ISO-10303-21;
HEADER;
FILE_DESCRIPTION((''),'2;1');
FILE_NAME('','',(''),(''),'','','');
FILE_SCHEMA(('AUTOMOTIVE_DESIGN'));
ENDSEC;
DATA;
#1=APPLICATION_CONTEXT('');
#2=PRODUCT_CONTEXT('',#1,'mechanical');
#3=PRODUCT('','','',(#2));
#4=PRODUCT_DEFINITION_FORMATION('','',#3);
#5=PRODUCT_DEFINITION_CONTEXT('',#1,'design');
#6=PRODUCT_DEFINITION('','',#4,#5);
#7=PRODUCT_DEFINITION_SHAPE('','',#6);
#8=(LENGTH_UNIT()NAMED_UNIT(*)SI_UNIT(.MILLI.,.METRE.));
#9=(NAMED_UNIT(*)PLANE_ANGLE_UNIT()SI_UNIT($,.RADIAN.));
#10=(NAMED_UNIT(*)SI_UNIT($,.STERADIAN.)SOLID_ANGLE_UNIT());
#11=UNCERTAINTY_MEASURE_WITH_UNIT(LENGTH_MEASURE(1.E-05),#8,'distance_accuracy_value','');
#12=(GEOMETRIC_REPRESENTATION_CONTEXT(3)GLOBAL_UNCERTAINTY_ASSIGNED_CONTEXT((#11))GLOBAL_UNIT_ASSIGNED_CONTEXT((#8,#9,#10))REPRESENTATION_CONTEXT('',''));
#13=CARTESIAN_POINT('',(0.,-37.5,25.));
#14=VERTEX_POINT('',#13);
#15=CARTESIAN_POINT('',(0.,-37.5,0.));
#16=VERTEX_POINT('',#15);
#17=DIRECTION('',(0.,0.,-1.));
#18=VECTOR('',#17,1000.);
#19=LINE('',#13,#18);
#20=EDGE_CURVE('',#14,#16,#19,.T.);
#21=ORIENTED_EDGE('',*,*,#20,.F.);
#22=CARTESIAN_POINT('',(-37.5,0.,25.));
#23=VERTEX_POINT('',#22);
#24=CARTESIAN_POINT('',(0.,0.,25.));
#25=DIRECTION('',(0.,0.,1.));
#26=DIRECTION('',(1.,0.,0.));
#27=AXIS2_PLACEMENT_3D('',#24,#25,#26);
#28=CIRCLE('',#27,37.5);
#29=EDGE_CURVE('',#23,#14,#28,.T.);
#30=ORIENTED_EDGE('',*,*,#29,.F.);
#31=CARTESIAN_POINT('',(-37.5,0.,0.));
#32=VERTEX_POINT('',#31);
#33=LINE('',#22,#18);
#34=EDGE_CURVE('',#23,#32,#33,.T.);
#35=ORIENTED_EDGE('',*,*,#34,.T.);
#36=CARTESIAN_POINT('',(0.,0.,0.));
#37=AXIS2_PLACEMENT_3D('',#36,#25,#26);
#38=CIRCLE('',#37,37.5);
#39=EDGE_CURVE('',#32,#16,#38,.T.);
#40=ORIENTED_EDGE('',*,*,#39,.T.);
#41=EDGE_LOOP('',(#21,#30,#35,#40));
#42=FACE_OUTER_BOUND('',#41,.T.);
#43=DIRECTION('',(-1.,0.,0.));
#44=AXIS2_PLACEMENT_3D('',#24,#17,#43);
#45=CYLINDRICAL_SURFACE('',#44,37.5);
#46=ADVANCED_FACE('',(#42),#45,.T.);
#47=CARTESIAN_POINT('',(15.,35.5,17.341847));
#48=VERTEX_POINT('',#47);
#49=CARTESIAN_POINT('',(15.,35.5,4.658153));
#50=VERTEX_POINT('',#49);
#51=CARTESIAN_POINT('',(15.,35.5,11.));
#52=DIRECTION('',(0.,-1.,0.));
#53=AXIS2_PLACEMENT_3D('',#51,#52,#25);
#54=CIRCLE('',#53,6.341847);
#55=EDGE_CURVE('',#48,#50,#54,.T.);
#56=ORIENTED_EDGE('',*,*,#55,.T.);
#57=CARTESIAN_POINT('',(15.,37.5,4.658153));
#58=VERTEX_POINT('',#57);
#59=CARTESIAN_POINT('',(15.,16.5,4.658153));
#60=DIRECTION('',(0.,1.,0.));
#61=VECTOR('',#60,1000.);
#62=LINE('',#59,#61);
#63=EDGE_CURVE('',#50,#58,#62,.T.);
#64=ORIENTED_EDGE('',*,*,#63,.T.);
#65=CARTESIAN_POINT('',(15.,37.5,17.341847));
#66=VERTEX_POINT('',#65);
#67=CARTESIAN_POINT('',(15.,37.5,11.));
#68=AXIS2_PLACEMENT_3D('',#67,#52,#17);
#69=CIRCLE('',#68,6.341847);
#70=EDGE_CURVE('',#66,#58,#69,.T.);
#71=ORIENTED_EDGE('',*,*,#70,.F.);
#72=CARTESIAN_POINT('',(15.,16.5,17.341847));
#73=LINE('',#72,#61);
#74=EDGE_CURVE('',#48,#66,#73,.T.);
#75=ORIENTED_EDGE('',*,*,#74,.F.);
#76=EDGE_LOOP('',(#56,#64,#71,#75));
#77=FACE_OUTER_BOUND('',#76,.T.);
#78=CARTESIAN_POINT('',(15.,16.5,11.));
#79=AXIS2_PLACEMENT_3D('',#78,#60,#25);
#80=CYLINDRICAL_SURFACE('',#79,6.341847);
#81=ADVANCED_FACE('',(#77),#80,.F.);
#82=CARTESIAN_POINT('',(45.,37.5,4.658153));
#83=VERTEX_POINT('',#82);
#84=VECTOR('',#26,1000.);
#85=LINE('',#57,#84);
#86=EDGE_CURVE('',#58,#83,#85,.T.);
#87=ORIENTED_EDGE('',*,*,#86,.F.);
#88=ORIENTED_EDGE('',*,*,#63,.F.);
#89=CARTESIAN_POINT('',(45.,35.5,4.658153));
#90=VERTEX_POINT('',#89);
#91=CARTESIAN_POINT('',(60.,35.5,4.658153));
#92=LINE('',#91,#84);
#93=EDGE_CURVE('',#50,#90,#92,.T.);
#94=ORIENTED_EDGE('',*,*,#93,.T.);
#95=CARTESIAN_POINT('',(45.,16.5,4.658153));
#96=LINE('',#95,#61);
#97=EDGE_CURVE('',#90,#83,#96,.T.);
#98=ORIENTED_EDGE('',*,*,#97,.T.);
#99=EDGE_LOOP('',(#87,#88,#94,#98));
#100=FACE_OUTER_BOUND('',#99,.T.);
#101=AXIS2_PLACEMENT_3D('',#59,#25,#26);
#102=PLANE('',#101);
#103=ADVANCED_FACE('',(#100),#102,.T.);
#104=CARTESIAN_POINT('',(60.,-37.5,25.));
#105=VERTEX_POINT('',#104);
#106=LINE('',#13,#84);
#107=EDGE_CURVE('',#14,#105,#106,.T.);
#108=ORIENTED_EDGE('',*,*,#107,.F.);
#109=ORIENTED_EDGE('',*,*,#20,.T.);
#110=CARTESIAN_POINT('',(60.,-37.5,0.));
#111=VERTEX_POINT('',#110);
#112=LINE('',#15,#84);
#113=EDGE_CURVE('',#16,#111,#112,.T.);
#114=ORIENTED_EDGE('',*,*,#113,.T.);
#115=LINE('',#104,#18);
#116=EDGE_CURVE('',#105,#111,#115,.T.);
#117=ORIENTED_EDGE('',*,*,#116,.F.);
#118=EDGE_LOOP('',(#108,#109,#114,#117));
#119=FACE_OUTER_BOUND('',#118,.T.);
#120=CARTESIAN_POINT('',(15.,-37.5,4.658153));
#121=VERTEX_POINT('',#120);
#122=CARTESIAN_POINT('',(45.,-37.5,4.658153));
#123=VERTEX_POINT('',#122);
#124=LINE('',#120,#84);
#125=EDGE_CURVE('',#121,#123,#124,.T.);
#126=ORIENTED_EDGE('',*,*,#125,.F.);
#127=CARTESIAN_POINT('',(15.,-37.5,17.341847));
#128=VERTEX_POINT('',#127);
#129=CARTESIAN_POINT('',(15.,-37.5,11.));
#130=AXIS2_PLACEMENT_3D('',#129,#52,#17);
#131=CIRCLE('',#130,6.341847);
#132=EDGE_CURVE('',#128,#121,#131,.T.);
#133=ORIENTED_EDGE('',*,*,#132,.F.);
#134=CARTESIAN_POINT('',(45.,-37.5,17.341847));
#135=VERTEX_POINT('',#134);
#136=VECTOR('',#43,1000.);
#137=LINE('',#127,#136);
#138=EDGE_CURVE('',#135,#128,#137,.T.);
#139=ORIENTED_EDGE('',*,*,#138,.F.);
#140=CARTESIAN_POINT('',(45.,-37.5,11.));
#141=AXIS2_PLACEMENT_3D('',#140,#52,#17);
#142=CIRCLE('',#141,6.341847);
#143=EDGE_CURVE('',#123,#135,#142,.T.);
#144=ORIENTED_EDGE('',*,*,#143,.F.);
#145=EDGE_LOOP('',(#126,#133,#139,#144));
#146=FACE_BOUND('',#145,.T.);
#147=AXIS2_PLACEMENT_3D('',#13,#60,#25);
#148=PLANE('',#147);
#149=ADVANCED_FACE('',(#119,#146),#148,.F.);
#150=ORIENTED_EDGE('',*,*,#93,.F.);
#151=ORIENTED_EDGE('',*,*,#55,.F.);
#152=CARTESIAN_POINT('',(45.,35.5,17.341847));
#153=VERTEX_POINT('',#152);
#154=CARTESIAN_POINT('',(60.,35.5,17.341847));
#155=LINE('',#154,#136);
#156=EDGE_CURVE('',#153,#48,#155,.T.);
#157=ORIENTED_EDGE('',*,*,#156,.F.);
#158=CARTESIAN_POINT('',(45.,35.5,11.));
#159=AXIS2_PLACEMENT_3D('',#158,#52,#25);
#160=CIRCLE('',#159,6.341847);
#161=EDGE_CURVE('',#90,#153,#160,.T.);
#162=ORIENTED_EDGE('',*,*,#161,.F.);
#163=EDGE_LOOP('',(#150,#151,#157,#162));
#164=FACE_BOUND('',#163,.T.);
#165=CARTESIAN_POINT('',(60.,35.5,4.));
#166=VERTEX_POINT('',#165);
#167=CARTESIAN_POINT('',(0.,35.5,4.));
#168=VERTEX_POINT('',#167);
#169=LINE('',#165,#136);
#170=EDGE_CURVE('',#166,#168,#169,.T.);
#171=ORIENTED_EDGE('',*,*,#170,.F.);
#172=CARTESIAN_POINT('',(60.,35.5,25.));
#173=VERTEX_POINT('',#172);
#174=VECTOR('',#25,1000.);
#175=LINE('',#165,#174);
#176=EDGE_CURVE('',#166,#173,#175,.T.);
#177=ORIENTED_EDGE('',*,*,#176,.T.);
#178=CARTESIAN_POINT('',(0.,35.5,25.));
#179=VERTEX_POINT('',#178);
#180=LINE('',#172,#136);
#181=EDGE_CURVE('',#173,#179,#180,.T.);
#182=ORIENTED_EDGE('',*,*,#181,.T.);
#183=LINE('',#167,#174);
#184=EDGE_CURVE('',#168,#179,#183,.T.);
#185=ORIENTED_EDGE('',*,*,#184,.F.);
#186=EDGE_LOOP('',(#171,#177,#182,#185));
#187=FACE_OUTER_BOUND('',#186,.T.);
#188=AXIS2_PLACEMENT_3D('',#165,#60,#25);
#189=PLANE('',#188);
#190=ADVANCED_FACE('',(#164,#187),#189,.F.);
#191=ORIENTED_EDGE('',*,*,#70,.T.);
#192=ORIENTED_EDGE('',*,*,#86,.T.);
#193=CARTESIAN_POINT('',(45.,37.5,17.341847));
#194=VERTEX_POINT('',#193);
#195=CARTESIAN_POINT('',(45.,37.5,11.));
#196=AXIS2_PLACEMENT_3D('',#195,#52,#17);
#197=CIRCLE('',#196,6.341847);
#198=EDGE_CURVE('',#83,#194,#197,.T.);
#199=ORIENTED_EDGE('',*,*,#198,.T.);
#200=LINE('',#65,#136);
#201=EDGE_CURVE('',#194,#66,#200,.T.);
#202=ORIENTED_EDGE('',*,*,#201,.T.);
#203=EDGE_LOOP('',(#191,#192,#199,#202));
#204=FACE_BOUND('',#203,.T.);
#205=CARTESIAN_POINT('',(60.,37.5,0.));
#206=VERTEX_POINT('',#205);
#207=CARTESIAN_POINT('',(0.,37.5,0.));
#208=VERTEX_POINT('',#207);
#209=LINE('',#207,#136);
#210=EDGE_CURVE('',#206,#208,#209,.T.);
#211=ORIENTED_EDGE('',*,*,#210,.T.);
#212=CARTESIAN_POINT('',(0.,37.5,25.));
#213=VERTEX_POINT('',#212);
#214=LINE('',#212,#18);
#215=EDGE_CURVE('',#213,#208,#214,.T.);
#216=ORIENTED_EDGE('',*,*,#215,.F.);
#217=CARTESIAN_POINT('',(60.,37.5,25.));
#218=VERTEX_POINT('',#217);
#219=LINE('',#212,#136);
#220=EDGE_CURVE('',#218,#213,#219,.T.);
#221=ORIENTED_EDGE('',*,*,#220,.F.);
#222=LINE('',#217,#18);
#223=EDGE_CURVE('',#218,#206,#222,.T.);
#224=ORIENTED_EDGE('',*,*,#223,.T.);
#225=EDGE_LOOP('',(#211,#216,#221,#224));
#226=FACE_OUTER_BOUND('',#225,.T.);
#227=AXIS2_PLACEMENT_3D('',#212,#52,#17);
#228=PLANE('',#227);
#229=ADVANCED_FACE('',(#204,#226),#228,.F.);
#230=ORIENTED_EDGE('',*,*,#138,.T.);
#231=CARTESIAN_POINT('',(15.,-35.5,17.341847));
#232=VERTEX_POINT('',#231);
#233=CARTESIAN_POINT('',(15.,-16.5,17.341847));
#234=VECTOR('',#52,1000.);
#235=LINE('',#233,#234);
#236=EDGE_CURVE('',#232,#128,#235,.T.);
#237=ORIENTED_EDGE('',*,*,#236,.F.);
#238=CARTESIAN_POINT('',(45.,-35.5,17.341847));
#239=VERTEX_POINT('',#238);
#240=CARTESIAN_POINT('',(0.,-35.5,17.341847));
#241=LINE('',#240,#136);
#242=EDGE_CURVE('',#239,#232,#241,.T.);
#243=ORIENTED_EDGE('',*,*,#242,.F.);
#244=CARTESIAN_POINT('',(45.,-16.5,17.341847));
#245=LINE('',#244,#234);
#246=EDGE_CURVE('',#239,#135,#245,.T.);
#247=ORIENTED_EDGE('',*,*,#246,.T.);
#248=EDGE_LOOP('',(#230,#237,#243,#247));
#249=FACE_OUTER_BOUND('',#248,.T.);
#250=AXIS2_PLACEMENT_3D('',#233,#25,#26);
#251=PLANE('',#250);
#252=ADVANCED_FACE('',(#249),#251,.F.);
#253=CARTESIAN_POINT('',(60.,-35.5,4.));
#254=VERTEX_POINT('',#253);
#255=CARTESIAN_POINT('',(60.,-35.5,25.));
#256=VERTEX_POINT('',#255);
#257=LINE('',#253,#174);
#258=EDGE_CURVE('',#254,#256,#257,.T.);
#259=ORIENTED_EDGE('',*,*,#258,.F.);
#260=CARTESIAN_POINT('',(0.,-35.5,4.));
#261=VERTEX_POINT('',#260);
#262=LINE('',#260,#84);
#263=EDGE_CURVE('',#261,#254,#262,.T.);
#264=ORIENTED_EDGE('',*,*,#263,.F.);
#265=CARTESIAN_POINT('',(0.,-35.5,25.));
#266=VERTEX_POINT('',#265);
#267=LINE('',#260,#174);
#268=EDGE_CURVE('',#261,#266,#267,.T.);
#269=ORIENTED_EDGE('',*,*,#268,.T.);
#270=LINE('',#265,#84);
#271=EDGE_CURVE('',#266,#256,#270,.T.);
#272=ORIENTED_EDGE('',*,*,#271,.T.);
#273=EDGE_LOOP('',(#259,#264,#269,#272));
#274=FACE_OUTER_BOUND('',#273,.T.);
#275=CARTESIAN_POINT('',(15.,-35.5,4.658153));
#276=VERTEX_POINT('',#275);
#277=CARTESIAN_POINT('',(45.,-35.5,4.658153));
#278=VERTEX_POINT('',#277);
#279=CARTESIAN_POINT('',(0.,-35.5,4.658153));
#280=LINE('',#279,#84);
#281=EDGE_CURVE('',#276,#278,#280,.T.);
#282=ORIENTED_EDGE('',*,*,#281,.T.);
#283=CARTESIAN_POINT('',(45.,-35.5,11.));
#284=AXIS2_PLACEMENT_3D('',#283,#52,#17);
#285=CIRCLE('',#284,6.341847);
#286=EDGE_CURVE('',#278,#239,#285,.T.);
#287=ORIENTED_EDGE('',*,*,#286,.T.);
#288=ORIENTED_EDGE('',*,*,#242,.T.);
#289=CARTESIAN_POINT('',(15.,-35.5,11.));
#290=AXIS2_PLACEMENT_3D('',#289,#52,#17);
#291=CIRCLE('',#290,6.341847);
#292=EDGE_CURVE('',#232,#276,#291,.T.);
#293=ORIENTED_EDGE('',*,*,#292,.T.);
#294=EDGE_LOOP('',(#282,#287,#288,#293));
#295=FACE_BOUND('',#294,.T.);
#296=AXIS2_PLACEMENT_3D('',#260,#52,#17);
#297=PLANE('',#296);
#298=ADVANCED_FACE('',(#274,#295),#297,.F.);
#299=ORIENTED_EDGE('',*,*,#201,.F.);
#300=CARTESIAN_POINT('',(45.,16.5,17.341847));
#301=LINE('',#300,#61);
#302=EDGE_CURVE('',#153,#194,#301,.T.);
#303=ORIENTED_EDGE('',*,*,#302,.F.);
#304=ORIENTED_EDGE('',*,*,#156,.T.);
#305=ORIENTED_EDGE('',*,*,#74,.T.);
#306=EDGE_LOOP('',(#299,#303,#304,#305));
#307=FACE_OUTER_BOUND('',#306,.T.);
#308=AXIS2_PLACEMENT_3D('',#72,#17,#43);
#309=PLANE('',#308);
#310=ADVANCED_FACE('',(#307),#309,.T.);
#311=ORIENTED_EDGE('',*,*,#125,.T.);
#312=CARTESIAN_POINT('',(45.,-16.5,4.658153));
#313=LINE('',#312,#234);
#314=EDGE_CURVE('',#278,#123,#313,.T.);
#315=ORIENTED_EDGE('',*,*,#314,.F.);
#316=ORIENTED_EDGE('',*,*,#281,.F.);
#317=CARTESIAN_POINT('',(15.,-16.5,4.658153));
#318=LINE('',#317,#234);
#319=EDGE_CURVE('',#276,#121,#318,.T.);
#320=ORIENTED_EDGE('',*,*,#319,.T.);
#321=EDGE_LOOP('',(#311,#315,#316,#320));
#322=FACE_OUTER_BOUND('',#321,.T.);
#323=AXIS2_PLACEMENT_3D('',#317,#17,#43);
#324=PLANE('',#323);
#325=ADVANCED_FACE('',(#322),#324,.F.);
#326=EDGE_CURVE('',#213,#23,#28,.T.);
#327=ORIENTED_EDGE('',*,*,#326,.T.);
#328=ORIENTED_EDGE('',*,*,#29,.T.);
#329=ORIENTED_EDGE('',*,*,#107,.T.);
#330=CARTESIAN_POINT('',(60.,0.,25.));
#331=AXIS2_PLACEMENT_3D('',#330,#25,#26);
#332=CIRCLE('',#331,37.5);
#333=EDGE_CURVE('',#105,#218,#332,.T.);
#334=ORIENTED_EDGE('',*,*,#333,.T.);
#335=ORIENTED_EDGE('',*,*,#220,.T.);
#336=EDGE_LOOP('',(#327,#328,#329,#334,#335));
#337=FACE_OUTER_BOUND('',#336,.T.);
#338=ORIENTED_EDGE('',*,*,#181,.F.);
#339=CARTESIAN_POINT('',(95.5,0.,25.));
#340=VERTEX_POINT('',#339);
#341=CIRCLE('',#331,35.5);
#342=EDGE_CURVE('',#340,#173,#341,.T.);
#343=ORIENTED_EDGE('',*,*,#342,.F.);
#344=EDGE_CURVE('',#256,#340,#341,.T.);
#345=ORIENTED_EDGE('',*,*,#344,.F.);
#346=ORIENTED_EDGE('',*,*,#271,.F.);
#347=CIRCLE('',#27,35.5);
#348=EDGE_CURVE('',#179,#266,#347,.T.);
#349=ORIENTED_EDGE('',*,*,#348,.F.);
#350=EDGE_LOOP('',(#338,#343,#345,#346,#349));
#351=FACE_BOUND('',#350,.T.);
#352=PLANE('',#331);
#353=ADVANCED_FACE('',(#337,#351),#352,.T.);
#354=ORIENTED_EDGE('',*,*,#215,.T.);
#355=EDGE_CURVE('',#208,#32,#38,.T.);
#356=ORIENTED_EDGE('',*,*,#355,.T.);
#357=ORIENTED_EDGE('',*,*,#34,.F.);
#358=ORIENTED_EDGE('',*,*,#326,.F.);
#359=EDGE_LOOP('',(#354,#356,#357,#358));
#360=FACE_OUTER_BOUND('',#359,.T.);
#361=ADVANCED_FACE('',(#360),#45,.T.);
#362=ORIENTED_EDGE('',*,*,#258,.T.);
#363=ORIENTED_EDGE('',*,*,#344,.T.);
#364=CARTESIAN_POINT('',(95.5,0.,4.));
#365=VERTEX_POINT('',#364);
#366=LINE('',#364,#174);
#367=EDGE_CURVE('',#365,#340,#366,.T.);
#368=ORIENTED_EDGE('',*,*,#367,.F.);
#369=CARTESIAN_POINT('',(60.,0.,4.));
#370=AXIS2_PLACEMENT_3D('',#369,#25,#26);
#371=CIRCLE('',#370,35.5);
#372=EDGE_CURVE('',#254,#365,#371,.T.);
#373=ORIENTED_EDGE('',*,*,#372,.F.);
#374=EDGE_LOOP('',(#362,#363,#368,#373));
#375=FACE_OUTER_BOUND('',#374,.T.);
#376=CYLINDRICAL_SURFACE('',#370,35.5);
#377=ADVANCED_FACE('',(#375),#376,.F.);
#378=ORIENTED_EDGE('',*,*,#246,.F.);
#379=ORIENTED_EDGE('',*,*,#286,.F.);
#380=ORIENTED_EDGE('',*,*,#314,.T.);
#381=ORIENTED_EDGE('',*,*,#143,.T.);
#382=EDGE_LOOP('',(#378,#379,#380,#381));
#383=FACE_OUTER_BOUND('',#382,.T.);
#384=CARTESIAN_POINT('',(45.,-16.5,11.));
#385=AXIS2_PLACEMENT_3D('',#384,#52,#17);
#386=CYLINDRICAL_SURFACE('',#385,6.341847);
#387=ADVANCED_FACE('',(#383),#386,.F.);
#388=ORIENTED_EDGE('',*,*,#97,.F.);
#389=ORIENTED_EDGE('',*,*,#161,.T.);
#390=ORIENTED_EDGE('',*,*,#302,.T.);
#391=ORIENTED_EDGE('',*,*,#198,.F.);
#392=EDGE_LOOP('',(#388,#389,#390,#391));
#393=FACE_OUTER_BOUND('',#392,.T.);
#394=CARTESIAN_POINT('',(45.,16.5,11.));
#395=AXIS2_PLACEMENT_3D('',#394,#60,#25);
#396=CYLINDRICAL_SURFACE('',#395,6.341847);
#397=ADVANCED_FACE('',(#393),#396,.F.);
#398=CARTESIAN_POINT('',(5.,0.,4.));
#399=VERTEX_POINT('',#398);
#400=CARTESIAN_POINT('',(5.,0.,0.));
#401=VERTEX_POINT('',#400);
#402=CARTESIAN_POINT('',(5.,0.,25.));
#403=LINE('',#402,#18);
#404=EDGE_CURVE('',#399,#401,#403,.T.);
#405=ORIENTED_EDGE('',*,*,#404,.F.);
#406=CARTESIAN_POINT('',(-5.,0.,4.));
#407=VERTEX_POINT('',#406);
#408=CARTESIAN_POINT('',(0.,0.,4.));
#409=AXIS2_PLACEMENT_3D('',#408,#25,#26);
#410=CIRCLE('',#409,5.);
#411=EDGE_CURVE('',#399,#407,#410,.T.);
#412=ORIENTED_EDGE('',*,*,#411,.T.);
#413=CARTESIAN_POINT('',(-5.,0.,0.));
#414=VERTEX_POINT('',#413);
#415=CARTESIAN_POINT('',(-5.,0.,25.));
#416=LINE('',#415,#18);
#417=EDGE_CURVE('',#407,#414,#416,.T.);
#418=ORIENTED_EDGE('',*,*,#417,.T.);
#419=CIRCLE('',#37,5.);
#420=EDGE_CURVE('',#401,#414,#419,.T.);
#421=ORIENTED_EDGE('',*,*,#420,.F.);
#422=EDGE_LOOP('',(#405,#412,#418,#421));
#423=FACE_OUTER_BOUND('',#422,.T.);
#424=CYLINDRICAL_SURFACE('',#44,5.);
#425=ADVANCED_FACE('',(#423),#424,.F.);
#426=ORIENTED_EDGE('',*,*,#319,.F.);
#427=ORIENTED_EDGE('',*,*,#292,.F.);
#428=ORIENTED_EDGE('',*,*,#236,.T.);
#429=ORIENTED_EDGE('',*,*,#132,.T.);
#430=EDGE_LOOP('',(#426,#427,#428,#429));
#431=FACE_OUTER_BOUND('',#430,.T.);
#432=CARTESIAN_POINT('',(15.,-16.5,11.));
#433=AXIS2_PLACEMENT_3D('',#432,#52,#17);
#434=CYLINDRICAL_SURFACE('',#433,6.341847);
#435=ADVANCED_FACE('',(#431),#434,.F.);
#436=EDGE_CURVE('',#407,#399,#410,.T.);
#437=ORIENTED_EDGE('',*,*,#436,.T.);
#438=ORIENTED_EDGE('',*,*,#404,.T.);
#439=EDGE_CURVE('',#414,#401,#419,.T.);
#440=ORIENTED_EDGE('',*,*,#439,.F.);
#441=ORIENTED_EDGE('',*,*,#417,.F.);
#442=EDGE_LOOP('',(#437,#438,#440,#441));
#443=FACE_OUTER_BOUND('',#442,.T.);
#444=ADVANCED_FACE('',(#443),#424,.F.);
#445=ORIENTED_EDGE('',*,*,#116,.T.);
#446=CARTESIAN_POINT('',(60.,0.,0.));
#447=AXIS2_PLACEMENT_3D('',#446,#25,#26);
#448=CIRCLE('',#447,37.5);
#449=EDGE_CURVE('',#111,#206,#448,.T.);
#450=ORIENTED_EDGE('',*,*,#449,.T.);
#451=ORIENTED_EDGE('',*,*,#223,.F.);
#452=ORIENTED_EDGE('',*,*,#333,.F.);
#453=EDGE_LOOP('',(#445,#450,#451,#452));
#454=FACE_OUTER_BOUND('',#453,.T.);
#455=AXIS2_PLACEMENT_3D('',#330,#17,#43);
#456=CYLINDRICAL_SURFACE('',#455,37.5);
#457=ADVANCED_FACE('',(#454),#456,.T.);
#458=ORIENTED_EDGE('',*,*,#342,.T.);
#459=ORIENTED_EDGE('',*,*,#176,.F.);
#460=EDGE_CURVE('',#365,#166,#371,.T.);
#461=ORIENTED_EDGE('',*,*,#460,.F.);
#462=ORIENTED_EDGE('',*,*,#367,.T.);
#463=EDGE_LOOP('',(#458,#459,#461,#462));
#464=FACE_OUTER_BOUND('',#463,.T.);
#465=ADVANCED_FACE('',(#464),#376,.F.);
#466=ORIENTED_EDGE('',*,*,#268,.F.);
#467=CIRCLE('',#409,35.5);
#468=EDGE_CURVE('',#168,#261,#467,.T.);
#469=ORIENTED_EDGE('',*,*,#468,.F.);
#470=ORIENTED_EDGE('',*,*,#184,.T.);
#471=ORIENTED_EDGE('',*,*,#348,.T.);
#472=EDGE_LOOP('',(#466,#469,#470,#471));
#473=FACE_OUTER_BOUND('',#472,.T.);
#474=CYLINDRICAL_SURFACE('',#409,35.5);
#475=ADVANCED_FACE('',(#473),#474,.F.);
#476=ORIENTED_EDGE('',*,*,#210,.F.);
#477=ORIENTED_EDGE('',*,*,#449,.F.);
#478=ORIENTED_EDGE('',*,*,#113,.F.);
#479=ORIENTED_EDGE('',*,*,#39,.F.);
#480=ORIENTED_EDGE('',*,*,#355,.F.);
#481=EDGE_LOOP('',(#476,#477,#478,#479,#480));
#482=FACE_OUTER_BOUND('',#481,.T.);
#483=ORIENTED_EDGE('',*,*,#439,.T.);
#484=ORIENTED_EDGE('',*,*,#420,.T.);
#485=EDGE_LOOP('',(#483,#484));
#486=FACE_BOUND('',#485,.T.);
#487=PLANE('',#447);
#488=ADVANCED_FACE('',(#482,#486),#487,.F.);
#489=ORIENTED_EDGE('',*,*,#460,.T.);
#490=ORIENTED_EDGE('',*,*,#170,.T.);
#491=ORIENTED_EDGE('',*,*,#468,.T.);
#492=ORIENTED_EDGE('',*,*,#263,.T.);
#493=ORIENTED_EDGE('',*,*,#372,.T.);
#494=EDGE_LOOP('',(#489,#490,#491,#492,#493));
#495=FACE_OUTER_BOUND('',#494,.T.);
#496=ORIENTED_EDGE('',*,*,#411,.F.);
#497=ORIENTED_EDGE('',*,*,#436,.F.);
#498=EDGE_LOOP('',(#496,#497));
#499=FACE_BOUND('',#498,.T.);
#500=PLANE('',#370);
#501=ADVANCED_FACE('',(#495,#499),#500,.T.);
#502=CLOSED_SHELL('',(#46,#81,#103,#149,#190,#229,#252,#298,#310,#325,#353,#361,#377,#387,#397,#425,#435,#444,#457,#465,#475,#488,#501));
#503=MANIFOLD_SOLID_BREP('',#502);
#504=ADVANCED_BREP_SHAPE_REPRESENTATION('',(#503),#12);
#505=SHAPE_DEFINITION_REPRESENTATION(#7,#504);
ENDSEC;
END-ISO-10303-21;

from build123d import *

# Parameters (mm, degrees)
SKETCH1_R           = 5
BOSS_EXTRUDE1_DEPTH = 25
CUT_EXTRUDE1_DEPTH  = 21
CUT_EXTRUDE2_DEPTH  = 21


with BuildPart() as part:
    # Sketch1 → Boss-Extrude1 (new body)
    with BuildSketch(Plane.XY):
        with BuildLine():
            Line((0, 37.5), (60, 37.5))
            ThreePointArc((60, 37.5), (97.5, 0), (60, -37.5))
            Line((60, -37.5), (0, -37.5))
            ThreePointArc((0, -37.5), (-37.5, 0), (0, 37.5))
        make_face()
        Circle(SKETCH1_R, mode=Mode.SUBTRACT)
    extrude(amount=BOSS_EXTRUDE1_DEPTH)

    # Sketch2 → Cut-Extrude1 (cut)
    with BuildSketch(Plane.XY.offset(25)):
        with BuildLine():
            Line((60, 35.5), (0, 35.5))
            ThreePointArc((0, 35.5), (-35.5, 0), (0, -35.5))
            Line((0, -35.5), (60, -35.5))
            ThreePointArc((60, -35.5), (95.5, 0), (60, 35.5))
        make_face()
    extrude(amount=-CUT_EXTRUDE1_DEPTH, mode=Mode.SUBTRACT)

    # Sketch4 → Cut-Extrude2 (cut)
    with BuildSketch(Plane.XZ.offset(37.5)):
        with BuildLine():
            Line((15, 17.341846587), (45, 17.341846587))
            ThreePointArc((45, 17.341846587), (51.341846587, 11), (45, 4.658153413))
            Line((45, 4.658153413), (15, 4.658153413))
            ThreePointArc((15, 4.658153413), (8.658153413, 11), (15, 17.341846587))
        make_face()
    cut_extrude2 = extrude(amount=-CUT_EXTRUDE2_DEPTH, mode=Mode.SUBTRACT)

    # Mirror2: Cut-Extrude2 across plane
    add(cut_extrude2.mirror(Plane.ZX), mode=Mode.SUBTRACT)


solid = part.part
